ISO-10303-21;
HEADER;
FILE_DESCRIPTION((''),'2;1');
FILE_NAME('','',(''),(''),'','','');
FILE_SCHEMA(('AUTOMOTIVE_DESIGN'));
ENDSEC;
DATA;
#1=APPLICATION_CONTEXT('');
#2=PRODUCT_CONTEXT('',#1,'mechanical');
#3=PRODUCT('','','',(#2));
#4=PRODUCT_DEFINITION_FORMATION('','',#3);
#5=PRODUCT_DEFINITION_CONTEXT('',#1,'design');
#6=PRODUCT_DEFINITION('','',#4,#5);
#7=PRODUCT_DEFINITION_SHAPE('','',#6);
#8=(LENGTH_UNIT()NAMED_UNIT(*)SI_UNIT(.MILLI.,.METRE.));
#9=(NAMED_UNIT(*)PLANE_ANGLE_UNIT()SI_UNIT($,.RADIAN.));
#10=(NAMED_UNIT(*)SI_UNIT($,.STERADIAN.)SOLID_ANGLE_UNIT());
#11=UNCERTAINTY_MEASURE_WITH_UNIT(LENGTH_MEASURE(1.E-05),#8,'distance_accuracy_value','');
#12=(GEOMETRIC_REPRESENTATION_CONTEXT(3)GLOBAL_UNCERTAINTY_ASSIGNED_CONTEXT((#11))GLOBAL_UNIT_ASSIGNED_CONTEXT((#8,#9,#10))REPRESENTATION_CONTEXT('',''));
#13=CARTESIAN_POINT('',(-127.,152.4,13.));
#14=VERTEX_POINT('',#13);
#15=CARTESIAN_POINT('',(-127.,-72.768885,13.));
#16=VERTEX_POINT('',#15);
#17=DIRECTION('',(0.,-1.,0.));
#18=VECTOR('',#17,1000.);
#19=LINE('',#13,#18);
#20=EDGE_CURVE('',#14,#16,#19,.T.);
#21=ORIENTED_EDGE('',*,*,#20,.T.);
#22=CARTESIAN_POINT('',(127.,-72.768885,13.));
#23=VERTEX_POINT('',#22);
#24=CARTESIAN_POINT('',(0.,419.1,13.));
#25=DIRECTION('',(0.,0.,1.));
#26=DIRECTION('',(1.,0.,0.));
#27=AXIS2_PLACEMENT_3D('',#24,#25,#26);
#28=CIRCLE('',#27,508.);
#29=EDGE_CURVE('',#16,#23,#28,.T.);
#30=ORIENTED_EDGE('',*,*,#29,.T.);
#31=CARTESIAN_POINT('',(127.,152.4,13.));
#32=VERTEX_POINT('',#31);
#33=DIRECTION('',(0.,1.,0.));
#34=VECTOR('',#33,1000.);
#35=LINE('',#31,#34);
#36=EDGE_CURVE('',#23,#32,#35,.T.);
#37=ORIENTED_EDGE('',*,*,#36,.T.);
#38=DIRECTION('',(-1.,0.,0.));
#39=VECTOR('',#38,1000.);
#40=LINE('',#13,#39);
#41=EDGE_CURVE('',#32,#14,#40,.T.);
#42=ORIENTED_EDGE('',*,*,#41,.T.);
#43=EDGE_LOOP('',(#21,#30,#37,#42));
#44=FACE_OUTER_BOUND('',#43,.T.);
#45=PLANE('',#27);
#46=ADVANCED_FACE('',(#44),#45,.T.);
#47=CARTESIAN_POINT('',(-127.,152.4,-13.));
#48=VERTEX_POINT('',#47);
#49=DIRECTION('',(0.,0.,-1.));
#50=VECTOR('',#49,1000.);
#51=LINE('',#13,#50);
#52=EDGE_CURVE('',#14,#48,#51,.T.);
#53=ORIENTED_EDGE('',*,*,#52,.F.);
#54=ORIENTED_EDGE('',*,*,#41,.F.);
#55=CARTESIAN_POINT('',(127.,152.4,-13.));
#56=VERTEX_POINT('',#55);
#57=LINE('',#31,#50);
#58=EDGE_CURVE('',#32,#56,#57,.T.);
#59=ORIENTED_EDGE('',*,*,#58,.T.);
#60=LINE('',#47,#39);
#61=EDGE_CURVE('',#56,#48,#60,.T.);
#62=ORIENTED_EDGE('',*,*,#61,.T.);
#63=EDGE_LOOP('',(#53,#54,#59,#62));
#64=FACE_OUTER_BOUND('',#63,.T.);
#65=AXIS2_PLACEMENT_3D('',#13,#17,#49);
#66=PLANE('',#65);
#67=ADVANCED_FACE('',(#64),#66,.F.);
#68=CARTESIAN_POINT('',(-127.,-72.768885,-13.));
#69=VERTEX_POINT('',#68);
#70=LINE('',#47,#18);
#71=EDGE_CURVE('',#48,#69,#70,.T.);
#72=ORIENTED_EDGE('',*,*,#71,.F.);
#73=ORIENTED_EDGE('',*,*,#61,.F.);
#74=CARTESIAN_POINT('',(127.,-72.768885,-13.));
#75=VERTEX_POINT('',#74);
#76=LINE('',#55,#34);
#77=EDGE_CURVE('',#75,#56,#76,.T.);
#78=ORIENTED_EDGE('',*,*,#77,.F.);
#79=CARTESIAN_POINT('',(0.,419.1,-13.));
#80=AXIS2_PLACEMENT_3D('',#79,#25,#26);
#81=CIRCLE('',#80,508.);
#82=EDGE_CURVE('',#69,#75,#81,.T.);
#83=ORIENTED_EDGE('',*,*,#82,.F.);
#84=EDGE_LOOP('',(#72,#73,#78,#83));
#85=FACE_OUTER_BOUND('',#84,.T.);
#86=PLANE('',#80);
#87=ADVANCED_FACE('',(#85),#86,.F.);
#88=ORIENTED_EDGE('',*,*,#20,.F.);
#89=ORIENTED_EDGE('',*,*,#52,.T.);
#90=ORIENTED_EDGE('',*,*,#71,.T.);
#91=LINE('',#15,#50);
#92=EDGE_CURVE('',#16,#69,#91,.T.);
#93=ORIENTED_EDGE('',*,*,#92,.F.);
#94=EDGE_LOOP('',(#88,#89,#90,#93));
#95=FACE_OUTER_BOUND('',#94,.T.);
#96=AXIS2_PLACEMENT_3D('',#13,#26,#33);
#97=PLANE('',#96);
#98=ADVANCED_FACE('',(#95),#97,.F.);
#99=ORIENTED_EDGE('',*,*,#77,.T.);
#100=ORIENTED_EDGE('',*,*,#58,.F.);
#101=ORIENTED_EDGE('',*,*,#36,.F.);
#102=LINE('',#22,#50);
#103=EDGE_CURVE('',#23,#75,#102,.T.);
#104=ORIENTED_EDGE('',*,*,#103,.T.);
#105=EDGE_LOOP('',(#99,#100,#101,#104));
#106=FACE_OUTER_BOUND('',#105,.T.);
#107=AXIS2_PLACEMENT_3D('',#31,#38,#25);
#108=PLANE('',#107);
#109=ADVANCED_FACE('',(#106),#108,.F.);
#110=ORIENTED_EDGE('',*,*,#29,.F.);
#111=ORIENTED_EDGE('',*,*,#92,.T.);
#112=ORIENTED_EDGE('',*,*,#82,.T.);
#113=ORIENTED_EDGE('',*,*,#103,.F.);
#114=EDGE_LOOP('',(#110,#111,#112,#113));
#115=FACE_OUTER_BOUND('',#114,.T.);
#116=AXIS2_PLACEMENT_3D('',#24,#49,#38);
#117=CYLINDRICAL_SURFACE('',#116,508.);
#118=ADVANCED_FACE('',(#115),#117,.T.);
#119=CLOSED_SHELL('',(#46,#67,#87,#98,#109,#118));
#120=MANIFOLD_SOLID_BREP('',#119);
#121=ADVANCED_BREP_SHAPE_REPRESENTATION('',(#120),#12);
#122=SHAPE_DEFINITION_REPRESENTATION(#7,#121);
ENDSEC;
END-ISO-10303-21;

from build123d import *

# Parameters (mm, degrees)
BOSS_EXTRUDE1_DEPTH = 13


with BuildPart() as part:
    # Sketch1 → Boss-Extrude1 (new, symmetric)
    with BuildSketch(Plane.XY):
        with BuildLine():
            Line((-127, 152.4), (127, 152.4))
            Line((127, 152.4), (127, -72.768884968))
            ThreePointArc((127, -72.768884968), (0, -88.9), (-127, -72.768884968))
            Line((-127, -72.768884968), (-127, 152.4))
        make_face()
    extrude(amount=BOSS_EXTRUDE1_DEPTH, both=True)


solid = part.part
